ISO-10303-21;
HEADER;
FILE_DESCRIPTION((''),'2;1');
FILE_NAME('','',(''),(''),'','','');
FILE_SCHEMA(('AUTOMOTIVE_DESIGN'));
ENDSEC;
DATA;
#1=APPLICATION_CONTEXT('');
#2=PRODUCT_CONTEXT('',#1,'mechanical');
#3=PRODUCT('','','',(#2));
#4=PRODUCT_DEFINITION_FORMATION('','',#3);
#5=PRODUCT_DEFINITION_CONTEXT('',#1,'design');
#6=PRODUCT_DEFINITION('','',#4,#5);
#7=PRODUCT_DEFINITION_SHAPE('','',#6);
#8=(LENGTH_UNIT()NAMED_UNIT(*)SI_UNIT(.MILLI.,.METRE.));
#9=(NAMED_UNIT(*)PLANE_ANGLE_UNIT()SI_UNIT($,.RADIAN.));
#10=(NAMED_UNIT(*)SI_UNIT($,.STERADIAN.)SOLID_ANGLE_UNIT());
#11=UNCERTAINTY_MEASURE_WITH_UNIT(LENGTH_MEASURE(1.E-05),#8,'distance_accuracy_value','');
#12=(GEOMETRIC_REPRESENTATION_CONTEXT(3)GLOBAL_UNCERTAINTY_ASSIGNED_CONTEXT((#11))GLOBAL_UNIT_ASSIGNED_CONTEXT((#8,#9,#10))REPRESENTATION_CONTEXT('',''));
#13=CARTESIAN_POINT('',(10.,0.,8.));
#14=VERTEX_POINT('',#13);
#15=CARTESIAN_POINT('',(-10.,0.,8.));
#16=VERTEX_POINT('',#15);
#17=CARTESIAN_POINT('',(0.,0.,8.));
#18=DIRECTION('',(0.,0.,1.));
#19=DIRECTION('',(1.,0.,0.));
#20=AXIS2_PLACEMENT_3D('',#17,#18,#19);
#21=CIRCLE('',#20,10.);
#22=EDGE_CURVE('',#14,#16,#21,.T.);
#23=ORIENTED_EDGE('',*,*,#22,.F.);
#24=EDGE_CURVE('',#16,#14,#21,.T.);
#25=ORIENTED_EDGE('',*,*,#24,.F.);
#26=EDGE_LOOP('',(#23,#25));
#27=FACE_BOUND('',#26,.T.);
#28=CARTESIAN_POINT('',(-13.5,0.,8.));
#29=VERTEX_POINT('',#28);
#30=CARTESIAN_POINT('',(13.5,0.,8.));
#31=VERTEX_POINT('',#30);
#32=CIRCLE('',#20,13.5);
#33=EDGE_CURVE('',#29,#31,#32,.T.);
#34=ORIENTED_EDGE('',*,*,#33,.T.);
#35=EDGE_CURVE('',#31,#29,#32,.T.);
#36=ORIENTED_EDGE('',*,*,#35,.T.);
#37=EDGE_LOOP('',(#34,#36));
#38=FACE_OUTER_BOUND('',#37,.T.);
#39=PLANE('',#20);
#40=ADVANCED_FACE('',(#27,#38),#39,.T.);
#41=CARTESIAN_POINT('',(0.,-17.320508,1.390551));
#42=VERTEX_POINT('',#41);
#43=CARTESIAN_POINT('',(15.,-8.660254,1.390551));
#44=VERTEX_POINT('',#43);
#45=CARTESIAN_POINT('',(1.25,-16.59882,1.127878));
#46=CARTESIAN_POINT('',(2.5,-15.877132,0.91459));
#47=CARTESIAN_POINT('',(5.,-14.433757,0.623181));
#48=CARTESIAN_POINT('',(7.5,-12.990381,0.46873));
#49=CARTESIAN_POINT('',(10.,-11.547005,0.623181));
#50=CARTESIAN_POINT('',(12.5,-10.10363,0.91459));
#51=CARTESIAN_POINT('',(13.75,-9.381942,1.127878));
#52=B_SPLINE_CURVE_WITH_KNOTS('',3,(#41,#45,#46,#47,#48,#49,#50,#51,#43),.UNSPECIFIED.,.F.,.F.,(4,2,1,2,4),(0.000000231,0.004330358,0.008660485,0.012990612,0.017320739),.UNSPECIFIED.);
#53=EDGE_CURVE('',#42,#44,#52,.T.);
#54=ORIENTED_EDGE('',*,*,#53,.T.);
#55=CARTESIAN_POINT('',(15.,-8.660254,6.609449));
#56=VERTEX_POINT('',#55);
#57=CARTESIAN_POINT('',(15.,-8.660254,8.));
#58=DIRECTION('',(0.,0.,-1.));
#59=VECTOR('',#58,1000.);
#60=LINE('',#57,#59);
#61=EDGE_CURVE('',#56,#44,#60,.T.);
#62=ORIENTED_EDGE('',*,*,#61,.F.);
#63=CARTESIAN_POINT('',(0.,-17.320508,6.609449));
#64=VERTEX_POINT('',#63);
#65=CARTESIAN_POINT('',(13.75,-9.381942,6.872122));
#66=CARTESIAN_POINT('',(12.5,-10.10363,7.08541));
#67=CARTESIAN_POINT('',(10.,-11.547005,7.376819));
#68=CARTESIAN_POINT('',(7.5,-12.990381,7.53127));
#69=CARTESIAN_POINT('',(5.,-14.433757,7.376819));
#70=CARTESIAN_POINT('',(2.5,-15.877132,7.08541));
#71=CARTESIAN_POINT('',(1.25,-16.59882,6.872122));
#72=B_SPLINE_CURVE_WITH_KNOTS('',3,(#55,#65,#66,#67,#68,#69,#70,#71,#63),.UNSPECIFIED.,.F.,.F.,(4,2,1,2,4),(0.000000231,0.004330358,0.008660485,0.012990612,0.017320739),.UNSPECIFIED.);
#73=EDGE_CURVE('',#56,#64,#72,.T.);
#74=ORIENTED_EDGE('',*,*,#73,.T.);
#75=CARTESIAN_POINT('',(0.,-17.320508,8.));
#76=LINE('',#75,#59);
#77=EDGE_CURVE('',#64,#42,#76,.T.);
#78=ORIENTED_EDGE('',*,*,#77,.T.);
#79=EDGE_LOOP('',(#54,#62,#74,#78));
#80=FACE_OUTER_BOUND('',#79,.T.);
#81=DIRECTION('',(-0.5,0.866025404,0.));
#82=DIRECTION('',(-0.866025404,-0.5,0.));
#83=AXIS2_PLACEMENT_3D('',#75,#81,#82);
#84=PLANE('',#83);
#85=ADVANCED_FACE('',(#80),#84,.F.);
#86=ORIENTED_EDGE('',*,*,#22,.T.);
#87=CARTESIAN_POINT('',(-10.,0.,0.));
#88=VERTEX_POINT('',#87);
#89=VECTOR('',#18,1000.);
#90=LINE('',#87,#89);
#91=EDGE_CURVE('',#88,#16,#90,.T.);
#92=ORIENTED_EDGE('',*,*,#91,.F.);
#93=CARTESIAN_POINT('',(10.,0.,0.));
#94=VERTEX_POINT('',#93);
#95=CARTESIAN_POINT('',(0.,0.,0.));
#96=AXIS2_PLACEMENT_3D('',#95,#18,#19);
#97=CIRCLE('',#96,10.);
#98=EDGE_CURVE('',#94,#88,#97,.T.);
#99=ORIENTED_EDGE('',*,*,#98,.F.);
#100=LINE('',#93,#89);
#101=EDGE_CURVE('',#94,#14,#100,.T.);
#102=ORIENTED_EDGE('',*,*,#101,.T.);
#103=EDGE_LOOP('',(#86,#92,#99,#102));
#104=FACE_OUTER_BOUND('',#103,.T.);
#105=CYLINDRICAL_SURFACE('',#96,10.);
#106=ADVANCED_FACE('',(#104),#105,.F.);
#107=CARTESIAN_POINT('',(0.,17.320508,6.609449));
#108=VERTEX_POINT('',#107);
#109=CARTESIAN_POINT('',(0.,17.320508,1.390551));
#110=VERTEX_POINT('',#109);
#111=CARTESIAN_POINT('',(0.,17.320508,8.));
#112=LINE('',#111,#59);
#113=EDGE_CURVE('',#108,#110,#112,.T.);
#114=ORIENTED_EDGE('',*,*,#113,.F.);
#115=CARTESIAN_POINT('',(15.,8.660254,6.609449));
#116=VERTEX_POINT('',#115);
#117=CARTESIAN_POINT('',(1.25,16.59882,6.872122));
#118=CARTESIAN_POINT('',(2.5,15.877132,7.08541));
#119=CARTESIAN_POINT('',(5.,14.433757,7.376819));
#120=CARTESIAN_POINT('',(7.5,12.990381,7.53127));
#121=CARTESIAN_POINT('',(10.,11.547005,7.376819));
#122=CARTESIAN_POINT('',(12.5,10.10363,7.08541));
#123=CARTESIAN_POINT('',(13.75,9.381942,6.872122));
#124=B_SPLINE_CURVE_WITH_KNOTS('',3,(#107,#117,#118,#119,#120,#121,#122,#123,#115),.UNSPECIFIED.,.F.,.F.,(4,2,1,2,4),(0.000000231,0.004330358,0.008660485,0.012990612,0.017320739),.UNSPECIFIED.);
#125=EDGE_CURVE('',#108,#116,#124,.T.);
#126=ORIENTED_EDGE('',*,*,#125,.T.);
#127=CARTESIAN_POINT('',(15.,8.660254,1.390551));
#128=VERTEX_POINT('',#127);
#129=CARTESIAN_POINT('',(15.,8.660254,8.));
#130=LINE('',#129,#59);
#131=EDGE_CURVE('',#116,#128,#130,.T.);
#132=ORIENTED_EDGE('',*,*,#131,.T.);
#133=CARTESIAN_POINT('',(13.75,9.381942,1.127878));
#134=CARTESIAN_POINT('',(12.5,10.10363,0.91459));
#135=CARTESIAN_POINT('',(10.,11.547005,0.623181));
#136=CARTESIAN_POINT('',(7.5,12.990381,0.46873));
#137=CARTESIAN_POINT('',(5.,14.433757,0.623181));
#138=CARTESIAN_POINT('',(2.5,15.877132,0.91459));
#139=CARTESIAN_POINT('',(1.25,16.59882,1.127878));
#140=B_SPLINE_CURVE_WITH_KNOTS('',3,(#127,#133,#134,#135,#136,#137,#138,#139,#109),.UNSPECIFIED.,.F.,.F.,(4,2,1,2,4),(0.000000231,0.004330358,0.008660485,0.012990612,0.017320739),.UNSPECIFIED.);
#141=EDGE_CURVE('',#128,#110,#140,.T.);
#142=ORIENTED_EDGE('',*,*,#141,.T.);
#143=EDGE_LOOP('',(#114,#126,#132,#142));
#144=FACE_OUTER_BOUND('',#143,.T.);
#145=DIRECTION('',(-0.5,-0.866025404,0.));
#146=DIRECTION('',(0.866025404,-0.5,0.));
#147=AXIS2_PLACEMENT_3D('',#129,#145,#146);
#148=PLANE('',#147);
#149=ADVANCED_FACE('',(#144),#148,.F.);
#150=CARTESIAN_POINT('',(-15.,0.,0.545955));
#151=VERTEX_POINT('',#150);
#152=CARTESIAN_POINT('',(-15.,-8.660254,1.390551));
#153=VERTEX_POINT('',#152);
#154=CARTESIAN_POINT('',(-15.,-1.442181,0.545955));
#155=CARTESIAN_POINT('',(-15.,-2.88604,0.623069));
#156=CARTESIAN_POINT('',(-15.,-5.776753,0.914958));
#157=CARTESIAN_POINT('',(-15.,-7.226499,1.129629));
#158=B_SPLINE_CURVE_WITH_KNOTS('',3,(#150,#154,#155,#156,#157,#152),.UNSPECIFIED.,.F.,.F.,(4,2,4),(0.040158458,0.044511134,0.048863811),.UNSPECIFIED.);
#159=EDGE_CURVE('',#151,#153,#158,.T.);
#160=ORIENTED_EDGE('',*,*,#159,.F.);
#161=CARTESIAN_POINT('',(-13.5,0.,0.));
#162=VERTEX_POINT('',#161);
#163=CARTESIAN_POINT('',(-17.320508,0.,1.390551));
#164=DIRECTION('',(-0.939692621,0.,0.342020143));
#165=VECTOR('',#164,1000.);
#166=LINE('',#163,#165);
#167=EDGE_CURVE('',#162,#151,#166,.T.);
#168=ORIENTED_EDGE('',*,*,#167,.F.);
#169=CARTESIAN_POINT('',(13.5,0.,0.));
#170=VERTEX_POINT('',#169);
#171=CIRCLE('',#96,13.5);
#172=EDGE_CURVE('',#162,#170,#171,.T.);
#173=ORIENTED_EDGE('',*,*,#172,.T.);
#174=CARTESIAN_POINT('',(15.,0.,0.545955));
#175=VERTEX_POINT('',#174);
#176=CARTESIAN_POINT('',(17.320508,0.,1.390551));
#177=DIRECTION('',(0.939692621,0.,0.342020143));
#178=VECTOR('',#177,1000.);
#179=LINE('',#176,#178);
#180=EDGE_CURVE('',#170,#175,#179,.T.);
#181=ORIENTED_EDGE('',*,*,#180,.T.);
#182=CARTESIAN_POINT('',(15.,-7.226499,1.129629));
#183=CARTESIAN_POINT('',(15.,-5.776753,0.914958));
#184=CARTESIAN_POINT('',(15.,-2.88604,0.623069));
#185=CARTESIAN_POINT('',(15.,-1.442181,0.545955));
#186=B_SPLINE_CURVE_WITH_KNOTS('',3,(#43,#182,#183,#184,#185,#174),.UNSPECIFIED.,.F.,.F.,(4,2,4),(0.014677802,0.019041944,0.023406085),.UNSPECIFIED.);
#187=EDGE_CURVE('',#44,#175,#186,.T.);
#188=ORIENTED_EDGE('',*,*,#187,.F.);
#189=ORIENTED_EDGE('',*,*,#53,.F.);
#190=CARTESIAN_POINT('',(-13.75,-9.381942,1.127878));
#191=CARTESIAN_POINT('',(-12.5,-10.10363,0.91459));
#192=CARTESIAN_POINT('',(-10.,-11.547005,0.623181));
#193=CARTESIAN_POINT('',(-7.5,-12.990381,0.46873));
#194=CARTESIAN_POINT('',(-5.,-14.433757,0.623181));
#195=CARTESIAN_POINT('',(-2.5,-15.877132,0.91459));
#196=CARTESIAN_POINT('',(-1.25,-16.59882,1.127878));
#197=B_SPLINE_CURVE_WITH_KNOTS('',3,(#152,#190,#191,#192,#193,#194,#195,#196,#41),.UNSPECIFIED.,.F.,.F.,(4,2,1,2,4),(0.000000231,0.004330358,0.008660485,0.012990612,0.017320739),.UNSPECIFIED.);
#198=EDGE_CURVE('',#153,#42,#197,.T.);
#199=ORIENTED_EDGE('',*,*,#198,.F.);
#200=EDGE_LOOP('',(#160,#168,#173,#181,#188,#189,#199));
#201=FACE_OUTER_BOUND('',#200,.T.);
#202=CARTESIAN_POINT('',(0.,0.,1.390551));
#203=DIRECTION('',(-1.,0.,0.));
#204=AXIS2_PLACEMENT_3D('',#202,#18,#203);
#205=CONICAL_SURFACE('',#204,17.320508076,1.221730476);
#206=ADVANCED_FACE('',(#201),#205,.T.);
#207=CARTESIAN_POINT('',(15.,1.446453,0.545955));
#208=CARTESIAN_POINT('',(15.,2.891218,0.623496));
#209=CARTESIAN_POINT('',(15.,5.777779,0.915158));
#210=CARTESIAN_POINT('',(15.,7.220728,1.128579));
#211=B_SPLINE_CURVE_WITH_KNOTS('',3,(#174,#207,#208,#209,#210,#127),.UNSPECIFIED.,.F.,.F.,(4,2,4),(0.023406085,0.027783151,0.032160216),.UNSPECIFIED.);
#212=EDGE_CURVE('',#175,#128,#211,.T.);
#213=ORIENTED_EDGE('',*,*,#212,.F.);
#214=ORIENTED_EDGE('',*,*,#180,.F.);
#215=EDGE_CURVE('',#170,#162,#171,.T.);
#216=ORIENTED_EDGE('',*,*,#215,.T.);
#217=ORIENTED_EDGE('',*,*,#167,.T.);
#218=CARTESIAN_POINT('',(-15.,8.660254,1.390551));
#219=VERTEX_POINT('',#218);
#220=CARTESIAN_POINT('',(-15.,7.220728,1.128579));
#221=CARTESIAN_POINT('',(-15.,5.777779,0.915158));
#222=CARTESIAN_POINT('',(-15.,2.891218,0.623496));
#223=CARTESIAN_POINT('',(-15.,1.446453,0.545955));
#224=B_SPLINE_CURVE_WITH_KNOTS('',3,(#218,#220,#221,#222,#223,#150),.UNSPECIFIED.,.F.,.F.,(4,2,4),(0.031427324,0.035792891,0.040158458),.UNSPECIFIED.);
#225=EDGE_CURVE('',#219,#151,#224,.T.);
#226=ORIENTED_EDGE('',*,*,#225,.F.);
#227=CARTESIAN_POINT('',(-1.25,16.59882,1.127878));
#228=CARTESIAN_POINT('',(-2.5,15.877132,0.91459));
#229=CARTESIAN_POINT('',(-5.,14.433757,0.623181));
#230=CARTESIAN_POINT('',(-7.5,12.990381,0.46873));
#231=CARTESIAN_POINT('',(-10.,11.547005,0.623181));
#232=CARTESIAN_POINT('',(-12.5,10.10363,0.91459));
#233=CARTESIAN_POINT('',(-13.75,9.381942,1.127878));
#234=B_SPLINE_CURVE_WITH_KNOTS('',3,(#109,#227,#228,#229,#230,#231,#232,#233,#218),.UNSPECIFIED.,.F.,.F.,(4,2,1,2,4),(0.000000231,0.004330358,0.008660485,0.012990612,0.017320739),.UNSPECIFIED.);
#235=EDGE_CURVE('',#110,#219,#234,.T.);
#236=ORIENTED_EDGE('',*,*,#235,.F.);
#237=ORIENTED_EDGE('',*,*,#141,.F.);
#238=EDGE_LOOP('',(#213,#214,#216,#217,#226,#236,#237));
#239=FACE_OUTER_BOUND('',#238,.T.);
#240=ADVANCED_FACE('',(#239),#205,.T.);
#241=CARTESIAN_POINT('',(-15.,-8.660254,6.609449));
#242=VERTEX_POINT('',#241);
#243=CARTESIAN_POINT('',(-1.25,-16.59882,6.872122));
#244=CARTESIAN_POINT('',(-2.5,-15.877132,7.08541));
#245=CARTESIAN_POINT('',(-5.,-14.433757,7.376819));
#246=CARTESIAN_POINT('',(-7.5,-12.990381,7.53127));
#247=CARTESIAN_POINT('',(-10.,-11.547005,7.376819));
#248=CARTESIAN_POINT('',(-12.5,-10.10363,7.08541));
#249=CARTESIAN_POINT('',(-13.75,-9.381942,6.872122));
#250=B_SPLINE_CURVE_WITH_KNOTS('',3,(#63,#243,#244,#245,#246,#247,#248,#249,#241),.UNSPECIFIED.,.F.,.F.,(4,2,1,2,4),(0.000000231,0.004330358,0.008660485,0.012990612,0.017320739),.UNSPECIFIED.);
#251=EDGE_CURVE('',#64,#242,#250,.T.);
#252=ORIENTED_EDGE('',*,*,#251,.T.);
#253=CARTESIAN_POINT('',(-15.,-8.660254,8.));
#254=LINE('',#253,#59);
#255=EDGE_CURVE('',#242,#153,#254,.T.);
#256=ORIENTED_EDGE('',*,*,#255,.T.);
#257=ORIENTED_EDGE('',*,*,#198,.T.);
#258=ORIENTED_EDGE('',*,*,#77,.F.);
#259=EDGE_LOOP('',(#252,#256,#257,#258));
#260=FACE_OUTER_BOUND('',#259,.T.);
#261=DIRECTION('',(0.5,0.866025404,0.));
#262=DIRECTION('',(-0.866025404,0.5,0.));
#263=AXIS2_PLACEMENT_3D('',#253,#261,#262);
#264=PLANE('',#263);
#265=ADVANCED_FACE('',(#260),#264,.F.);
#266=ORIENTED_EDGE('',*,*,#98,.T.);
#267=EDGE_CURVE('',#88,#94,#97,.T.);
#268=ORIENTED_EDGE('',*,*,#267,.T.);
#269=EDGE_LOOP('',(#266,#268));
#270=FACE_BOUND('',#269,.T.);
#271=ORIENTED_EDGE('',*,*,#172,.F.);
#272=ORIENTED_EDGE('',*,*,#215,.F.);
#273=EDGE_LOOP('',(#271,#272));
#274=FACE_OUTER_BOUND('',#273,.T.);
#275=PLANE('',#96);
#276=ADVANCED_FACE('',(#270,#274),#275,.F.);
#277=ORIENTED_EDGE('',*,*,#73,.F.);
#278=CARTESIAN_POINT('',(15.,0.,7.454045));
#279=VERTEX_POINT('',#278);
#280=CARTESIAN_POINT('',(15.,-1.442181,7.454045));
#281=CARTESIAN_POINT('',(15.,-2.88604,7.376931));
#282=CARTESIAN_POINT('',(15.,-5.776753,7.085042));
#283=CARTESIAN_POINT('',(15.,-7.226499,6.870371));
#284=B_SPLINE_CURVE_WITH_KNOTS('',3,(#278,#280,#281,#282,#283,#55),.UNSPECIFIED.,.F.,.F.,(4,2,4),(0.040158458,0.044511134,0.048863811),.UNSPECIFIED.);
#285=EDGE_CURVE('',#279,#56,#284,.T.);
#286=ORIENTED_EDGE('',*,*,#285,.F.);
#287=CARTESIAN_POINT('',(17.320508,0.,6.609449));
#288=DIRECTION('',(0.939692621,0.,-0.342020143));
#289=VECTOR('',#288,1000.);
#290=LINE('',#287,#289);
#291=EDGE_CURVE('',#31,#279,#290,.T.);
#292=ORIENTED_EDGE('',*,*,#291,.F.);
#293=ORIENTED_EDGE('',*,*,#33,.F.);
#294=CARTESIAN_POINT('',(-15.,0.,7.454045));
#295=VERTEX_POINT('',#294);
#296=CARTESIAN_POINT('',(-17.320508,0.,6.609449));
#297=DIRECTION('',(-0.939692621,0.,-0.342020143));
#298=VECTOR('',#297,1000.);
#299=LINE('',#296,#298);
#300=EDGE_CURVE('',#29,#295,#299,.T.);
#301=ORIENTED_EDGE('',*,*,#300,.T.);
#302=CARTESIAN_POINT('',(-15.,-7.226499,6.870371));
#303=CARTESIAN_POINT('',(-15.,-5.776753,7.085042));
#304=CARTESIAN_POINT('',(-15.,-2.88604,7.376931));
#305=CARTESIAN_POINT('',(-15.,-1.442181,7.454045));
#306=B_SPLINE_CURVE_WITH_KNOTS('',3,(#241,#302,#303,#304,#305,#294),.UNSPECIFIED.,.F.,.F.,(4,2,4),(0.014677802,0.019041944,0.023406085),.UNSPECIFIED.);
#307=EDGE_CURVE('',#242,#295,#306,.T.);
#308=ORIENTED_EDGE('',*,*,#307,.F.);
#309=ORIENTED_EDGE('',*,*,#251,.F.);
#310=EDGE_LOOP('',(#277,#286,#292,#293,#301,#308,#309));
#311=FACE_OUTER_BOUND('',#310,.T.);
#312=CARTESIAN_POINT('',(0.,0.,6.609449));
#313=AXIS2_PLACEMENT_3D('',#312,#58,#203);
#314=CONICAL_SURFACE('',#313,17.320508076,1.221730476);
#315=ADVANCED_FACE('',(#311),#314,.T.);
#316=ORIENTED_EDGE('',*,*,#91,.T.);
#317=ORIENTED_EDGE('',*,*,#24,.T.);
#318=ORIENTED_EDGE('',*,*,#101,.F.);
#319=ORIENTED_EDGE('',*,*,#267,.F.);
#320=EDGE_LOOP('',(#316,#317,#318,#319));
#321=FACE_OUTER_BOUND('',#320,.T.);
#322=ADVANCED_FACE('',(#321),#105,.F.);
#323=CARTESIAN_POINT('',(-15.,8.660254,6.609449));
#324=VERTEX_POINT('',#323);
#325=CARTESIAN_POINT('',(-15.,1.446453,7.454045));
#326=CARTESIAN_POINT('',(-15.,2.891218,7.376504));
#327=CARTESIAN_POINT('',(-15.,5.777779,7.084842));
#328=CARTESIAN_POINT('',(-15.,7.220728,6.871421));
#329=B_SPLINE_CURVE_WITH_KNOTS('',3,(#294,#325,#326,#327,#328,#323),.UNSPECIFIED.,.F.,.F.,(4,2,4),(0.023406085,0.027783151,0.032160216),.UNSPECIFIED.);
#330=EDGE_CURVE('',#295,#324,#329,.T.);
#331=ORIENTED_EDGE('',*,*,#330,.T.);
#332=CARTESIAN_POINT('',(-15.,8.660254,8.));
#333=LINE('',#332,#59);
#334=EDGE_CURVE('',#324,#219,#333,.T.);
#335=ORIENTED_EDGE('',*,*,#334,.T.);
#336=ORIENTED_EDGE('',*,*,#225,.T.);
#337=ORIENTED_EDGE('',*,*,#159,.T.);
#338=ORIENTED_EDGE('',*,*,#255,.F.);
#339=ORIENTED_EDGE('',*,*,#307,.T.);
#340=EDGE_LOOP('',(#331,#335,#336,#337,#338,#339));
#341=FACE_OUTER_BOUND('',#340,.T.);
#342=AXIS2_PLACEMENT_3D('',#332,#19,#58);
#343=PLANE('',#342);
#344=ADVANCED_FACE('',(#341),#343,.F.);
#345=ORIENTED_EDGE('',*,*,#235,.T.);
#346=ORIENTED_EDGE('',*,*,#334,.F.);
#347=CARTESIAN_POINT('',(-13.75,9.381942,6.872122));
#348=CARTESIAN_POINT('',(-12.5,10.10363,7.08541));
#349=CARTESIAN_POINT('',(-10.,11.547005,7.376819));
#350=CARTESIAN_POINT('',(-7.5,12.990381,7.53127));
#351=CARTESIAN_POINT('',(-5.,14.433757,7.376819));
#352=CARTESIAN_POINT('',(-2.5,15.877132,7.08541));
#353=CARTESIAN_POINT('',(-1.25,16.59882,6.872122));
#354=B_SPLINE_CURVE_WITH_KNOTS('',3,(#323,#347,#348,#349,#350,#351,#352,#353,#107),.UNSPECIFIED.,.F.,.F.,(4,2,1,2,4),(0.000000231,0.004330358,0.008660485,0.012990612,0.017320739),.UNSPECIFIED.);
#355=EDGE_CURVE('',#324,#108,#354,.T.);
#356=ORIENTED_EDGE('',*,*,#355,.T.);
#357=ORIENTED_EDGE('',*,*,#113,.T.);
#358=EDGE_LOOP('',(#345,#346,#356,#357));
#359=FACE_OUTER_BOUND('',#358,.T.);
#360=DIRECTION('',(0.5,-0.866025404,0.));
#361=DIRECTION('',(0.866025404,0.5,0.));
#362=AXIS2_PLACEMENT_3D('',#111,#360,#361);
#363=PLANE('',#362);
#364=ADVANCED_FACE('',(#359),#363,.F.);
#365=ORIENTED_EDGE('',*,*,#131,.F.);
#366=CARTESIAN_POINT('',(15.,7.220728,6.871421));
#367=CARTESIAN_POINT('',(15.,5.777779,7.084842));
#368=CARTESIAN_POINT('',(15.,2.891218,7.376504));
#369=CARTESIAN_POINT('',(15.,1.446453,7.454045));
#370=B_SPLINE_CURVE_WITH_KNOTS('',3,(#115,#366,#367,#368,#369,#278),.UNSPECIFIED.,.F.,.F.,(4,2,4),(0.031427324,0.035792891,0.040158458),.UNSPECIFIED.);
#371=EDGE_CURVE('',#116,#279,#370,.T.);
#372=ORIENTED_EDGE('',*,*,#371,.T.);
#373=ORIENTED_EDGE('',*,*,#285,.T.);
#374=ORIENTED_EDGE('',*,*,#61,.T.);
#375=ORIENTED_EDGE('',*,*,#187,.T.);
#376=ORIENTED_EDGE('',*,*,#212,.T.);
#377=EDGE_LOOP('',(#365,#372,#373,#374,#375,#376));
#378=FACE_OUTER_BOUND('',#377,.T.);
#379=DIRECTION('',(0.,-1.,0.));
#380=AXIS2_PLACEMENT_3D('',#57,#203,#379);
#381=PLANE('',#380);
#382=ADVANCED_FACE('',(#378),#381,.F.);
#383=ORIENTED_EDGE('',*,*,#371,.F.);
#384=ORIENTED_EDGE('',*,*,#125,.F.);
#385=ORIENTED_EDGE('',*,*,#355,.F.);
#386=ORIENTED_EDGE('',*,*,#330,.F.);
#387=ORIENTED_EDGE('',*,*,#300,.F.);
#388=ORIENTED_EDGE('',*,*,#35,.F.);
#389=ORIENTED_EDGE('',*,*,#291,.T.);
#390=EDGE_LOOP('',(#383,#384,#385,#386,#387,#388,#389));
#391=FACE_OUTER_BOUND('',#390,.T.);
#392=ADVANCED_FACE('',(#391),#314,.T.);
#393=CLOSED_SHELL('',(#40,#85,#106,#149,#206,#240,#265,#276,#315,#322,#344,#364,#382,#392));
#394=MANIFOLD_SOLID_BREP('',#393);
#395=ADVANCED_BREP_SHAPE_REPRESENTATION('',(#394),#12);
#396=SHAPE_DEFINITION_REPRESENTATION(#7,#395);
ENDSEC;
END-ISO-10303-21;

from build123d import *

# Parameters (mm, degrees)
EXTRUDE_1_DEPTH     = 8
SKETCH_5_R          = 10
CUT_EXTRUDE_1_DEPTH = 25.269322199


with BuildPart() as part:
    # 草图1 → 凸台-拉伸1 (new body)
    with BuildSketch(Plane.XY):
        Polygon((0, 17.320508076), (-15, 8.660254038), (-15, -8.660254038), (0, -17.320508076), (15, -8.660254038), (15, 8.660254038), align=None)
    extrude(amount=EXTRUDE_1_DEPTH)

    # 草图4 → 切除-旋转1 (revolve, cut)
    with BuildSketch(Plane(origin=(0, 0, 0), x_dir=(0, 0, -1), z_dir=(1, 0, 0)), mode=Mode.PRIVATE) as cut_revolve_1_sk:
        Polygon((-8, -13.5), (-6.609448781, -17.320508076), (-8, -17.320508076), align=None)
    cut_revolve_1 = revolve(cut_revolve_1_sk.sketch.rotate(Axis((0, 0, 8), (0, 0, -1)), 120.000000002), axis=Axis((0, 0, 8), (0, 0, -1)), mode=Mode.SUBTRACT)

    # 镜向1: 切除-旋转1 across plane
    add(cut_revolve_1.mirror(Plane.XY.offset(4)), mode=Mode.SUBTRACT)

    # 草图5 → 切除-拉伸1 (cut, through all)
    with BuildSketch(Plane.XY.offset(8)):
        Circle(SKETCH_5_R)
    extrude(amount=-CUT_EXTRUDE_1_DEPTH, mode=Mode.SUBTRACT)


solid = part.part
